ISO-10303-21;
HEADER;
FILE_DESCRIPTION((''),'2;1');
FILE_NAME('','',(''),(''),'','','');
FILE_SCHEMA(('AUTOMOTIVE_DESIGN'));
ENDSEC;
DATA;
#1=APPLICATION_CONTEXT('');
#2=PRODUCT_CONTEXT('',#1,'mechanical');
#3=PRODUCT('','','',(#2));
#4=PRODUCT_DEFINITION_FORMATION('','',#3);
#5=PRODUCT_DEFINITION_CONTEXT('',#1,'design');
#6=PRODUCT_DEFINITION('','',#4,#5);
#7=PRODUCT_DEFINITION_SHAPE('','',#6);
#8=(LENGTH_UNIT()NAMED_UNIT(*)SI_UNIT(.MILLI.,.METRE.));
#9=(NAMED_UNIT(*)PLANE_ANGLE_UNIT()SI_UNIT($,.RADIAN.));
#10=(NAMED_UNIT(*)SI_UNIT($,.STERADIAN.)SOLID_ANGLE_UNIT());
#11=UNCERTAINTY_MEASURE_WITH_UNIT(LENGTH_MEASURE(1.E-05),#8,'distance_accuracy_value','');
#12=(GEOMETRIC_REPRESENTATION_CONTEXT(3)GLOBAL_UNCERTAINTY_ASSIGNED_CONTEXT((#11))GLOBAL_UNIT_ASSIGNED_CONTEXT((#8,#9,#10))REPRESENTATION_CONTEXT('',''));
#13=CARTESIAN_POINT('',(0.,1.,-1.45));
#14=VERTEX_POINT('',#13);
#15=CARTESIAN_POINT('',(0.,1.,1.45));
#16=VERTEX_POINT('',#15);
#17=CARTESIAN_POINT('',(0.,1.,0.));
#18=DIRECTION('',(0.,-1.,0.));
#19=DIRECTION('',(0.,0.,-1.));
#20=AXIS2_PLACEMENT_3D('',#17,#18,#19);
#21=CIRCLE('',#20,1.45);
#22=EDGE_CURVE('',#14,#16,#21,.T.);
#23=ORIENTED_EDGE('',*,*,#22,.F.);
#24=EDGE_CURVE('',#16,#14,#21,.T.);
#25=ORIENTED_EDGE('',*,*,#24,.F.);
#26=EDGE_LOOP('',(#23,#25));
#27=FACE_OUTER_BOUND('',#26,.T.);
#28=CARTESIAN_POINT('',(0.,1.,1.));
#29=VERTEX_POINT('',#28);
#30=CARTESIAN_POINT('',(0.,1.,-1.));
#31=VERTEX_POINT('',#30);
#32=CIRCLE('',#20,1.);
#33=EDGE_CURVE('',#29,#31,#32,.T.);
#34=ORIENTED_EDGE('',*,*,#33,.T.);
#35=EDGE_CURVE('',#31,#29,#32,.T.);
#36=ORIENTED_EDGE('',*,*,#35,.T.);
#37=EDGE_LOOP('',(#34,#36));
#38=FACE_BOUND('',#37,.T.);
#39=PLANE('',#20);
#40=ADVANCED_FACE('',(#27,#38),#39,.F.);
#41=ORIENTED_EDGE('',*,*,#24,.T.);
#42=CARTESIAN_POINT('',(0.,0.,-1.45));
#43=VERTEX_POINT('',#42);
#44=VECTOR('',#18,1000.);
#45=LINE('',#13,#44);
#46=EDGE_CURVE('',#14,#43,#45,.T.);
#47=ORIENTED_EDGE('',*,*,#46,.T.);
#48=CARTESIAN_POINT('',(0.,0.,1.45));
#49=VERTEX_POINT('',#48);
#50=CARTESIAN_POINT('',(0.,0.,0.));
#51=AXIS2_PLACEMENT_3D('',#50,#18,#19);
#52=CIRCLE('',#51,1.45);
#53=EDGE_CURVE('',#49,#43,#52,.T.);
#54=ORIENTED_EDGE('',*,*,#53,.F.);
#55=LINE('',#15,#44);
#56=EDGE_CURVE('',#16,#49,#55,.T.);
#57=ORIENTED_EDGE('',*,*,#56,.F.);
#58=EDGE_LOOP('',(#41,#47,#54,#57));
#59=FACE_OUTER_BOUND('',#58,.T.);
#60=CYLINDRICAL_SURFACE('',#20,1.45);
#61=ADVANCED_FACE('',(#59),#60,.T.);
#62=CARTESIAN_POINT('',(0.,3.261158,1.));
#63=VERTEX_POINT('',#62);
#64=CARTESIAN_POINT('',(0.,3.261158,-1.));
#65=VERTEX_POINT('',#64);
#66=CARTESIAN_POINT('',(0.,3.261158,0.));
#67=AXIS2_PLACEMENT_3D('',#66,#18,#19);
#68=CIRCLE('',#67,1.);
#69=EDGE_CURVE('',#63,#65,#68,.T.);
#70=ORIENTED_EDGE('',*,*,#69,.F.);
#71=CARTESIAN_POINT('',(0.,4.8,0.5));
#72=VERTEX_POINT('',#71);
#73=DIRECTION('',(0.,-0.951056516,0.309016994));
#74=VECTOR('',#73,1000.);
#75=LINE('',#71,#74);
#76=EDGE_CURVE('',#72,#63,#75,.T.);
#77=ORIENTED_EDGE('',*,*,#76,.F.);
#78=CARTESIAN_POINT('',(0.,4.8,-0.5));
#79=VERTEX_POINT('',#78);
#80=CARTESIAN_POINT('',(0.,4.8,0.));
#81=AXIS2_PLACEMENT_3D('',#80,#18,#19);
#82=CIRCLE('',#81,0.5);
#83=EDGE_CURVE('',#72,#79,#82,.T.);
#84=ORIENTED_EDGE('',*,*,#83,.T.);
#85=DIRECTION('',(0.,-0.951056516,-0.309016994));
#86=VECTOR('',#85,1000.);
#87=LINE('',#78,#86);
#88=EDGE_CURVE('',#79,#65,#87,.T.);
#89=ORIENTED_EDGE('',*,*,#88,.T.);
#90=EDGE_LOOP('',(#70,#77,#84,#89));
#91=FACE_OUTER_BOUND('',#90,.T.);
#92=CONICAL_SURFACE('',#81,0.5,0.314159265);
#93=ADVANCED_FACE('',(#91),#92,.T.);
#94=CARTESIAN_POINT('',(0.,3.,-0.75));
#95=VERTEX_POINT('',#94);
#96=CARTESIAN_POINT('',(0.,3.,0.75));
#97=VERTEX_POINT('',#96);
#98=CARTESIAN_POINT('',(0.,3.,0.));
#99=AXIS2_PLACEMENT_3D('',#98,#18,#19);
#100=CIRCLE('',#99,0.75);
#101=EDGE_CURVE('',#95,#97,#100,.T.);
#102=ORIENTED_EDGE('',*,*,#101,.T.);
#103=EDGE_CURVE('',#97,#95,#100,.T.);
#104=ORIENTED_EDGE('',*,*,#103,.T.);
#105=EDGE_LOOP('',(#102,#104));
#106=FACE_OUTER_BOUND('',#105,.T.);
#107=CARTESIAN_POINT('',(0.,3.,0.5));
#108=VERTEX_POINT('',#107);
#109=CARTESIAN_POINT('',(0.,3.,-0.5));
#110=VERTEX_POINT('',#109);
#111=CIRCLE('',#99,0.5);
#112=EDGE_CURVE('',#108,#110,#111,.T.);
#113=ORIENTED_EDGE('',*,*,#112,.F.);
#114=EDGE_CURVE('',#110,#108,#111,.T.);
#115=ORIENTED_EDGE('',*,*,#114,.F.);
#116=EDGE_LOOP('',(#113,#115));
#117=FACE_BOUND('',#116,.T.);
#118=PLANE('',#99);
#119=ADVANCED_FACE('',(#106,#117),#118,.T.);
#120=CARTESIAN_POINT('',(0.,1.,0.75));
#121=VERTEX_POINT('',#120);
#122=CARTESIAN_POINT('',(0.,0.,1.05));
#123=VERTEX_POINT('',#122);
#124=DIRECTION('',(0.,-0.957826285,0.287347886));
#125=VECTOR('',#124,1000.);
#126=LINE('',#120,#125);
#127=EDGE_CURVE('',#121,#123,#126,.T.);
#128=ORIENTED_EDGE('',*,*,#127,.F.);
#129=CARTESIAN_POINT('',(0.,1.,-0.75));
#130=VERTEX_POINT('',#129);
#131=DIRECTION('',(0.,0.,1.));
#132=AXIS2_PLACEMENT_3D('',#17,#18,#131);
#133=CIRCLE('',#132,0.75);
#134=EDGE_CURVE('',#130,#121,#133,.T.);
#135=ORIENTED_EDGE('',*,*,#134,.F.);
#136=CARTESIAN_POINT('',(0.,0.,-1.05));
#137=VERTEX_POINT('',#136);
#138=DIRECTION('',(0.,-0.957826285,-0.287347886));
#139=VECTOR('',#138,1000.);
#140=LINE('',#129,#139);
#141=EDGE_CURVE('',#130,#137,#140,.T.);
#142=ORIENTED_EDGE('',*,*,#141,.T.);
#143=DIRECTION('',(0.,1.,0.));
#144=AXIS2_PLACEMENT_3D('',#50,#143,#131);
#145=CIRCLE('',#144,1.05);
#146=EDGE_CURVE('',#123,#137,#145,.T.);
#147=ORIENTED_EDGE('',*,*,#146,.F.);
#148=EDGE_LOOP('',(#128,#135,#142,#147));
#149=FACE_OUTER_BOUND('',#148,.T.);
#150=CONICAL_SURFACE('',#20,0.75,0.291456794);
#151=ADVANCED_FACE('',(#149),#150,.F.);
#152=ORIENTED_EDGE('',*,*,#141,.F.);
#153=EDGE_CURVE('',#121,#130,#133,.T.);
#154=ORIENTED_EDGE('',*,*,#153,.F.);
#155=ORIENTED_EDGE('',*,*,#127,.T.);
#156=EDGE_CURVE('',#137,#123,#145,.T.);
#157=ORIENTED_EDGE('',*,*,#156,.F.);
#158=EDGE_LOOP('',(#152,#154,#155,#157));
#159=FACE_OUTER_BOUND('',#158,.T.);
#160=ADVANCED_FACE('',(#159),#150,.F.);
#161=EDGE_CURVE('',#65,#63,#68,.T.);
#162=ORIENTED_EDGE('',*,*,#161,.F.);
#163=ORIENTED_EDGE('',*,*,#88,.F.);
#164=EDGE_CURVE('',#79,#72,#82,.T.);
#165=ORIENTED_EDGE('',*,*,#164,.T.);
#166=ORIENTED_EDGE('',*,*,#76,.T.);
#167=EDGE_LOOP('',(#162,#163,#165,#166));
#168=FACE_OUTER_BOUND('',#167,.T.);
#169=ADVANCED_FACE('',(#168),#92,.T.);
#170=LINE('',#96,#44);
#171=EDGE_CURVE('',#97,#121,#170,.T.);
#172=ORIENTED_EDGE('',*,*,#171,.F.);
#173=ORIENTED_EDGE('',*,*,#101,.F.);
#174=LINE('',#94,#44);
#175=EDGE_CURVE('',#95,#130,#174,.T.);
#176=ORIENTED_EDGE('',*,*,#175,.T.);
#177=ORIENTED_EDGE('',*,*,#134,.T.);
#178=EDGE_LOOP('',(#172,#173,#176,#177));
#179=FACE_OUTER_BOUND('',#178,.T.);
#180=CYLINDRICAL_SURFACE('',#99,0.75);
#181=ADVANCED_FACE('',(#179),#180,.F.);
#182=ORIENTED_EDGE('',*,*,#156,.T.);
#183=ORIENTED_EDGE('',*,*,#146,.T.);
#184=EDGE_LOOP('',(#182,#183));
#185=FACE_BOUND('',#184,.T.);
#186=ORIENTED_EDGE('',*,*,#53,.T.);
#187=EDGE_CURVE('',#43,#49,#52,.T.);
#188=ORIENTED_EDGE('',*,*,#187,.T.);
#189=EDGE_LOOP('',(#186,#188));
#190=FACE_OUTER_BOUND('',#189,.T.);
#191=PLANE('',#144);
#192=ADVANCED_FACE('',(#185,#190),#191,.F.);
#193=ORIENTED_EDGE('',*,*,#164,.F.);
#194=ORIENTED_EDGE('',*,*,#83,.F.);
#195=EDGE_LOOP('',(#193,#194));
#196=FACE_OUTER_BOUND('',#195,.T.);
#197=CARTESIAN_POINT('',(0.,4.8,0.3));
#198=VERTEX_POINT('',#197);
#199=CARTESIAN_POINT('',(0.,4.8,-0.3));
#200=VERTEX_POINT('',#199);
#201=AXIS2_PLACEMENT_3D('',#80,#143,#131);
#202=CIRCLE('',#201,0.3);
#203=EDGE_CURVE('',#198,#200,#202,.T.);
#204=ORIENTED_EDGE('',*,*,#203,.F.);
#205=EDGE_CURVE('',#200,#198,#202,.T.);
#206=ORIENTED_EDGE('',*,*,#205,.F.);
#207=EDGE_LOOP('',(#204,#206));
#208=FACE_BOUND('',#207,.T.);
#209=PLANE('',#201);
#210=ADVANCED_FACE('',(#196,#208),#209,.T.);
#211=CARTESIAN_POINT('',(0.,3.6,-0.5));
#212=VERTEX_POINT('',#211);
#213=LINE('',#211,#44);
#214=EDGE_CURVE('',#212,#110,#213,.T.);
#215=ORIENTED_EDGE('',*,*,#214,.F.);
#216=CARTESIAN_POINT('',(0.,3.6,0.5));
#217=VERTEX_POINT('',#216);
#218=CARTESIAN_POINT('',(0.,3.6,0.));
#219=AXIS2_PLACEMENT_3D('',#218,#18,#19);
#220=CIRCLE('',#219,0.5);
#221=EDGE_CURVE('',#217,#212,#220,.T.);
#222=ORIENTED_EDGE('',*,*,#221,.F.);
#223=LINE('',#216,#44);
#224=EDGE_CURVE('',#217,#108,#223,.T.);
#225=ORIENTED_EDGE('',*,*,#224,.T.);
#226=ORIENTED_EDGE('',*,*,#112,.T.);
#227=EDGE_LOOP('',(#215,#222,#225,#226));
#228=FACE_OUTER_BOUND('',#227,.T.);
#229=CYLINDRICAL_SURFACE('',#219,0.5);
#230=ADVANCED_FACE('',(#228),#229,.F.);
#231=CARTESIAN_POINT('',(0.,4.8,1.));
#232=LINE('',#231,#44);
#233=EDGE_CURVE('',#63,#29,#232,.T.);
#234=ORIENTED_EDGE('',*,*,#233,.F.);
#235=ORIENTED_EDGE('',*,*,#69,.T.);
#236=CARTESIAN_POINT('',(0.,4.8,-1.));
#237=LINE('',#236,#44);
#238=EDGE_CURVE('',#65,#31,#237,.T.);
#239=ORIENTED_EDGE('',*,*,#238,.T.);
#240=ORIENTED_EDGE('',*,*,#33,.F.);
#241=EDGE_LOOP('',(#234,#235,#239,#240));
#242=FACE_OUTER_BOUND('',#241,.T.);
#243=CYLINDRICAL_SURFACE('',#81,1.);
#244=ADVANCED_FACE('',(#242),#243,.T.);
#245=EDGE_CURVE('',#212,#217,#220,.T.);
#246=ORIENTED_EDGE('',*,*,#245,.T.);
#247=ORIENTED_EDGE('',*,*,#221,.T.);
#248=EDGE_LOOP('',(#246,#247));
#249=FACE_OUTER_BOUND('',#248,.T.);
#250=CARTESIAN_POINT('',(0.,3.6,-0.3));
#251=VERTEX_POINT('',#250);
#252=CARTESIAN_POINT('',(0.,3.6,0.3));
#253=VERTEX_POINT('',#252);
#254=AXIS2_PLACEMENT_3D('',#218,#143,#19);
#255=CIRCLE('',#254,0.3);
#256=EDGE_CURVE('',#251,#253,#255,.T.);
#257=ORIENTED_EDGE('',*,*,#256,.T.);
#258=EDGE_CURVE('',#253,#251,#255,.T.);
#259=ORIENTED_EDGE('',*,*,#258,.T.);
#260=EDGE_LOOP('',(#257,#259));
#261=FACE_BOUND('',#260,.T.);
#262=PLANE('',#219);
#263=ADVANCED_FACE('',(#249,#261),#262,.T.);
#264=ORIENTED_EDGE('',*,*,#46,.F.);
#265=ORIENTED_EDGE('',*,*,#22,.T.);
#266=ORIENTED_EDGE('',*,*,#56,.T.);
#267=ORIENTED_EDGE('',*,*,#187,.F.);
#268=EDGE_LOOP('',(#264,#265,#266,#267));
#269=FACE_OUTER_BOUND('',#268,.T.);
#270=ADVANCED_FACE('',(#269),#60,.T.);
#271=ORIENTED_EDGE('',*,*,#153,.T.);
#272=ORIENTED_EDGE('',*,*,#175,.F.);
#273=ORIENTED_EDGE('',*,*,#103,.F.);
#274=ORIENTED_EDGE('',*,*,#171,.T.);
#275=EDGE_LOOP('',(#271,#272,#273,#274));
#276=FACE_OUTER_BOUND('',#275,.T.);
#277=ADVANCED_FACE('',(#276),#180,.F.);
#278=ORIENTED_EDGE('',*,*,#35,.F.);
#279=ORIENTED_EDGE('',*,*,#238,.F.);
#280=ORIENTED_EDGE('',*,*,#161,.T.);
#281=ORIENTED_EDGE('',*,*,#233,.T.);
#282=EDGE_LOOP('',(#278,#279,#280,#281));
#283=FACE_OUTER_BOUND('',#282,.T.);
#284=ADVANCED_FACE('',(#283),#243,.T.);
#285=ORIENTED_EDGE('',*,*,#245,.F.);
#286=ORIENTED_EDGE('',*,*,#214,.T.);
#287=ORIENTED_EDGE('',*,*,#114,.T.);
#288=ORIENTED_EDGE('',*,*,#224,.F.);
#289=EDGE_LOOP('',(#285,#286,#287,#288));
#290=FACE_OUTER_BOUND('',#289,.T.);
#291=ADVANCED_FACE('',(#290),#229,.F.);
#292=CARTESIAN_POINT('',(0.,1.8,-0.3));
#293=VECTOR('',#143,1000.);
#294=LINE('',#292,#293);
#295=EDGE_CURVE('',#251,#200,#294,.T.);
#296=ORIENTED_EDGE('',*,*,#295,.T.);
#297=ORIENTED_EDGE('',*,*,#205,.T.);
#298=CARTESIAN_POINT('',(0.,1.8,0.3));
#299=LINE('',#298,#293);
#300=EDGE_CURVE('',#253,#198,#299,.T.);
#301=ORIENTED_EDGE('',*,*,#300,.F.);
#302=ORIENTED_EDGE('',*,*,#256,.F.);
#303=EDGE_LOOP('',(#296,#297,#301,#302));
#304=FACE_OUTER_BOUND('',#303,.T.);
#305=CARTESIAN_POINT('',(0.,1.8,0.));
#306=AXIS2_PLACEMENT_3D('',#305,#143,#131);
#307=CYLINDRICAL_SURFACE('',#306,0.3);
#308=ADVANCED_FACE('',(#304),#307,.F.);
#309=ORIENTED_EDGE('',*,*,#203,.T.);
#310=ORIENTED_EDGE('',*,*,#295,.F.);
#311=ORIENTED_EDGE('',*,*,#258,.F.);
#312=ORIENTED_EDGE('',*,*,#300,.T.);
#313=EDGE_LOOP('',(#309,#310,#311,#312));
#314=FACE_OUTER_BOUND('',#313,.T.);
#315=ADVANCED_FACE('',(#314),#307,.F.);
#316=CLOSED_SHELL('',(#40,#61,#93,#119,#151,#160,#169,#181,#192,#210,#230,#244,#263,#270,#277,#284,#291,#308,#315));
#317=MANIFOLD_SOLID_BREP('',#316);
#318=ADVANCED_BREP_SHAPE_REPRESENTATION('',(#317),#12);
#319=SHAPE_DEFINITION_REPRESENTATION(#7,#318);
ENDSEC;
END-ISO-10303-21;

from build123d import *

# Parameters (mm, degrees)
SKETCH1_R           = 1
BOSS_EXTRUDE1_DEPTH = 4.8
SKETCH3_R           = 0.75
CUT_EXTRUDE1_DEPTH  = 3
SKETCH4_R           = 0.3
CUT_EXTRUDE2_DEPTH  = 3
SKETCH5_R           = 0.5
CUT_EXTRUDE3_DEPTH  = 0.6
SKETCH6_R           = 1.45
SKETCH6_R_2         = 1
BOSS_EXTRUDE2_DEPTH = 1
CHAMFER1_SIZE       = 0.3
CHAMFER1_SIZE2      = 1


with BuildPart() as part:
    # Sketch1 → Boss-Extrude1 (new body)
    with BuildSketch(Plane(origin=(0, 0, 0), x_dir=(1, 0, 0), z_dir=(0, 1, 0))):
        with Locations(Location((0, 0, 0), (0, 0, 270))):
            Circle(SKETCH1_R)
    extrude(amount=BOSS_EXTRUDE1_DEPTH)

    # Sketch2 → Cut-Revolve1 (revolve, cut)
    with BuildSketch(Plane.XY, mode=Mode.PRIVATE) as cut_revolve1_sk:
        Polygon((0.5, 4.8), (1.621441373, 1.348558349), (1.621441373, 4.8), align=None)
    revolve(cut_revolve1_sk.sketch.rotate(Axis((0, 0, 0), (0, 1, 0)), 90), axis=Axis((0, 0, 0), (0, 1, 0)), mode=Mode.SUBTRACT)

    # Sketch3 → Cut-Extrude1 (cut)
    with BuildSketch(Plane.XZ):
        with Locations(Location((0, 0, 0), (0, 0, 270))):
            Circle(SKETCH3_R)
    extrude(amount=-CUT_EXTRUDE1_DEPTH, mode=Mode.SUBTRACT)

    # Sketch4 → Cut-Extrude2 (cut)
    with BuildSketch(Plane(origin=(0, 4.8, 0), x_dir=(1, 0, 0), z_dir=(0, 1, 0))):
        with Locations(Location((0, 0, 0), (0, 0, 270))):
            Circle(SKETCH4_R)
    extrude(amount=-CUT_EXTRUDE2_DEPTH, mode=Mode.SUBTRACT)

    # Sketch5 → Cut-Extrude3 (cut)
    with BuildSketch(Plane.XZ.offset(-3)):
        with Locations(Location((0, 0, 0), (0, 0, 270))):
            Circle(SKETCH5_R)
    extrude(amount=-CUT_EXTRUDE3_DEPTH, mode=Mode.SUBTRACT)

    # Sketch6 → Boss-Extrude2 (add)
    with BuildSketch(Plane.XZ):
        with Locations(Location((0, 0, 0), (0, 0, 270))):
            Circle(SKETCH6_R)
        with Locations(Location((0, 0, 0), (0, 0, 270))):
            Circle(SKETCH6_R_2, mode=Mode.SUBTRACT)
    extrude(amount=-BOSS_EXTRUDE2_DEPTH)

    # Chamfer1
    chamfer1_edges = [part.edges().sort_by_distance(p)[0] for p in [
        (0, 0, 0.75),
    ]]
    chamfer1_side = [part.faces().sort_by_distance(p)[0] for p in [
        (0, 0, 1.408987807),
    ]]
    chamfer(chamfer1_edges, length=CHAMFER1_SIZE, length2=CHAMFER1_SIZE2, reference=chamfer1_side[0])


solid = part.part
